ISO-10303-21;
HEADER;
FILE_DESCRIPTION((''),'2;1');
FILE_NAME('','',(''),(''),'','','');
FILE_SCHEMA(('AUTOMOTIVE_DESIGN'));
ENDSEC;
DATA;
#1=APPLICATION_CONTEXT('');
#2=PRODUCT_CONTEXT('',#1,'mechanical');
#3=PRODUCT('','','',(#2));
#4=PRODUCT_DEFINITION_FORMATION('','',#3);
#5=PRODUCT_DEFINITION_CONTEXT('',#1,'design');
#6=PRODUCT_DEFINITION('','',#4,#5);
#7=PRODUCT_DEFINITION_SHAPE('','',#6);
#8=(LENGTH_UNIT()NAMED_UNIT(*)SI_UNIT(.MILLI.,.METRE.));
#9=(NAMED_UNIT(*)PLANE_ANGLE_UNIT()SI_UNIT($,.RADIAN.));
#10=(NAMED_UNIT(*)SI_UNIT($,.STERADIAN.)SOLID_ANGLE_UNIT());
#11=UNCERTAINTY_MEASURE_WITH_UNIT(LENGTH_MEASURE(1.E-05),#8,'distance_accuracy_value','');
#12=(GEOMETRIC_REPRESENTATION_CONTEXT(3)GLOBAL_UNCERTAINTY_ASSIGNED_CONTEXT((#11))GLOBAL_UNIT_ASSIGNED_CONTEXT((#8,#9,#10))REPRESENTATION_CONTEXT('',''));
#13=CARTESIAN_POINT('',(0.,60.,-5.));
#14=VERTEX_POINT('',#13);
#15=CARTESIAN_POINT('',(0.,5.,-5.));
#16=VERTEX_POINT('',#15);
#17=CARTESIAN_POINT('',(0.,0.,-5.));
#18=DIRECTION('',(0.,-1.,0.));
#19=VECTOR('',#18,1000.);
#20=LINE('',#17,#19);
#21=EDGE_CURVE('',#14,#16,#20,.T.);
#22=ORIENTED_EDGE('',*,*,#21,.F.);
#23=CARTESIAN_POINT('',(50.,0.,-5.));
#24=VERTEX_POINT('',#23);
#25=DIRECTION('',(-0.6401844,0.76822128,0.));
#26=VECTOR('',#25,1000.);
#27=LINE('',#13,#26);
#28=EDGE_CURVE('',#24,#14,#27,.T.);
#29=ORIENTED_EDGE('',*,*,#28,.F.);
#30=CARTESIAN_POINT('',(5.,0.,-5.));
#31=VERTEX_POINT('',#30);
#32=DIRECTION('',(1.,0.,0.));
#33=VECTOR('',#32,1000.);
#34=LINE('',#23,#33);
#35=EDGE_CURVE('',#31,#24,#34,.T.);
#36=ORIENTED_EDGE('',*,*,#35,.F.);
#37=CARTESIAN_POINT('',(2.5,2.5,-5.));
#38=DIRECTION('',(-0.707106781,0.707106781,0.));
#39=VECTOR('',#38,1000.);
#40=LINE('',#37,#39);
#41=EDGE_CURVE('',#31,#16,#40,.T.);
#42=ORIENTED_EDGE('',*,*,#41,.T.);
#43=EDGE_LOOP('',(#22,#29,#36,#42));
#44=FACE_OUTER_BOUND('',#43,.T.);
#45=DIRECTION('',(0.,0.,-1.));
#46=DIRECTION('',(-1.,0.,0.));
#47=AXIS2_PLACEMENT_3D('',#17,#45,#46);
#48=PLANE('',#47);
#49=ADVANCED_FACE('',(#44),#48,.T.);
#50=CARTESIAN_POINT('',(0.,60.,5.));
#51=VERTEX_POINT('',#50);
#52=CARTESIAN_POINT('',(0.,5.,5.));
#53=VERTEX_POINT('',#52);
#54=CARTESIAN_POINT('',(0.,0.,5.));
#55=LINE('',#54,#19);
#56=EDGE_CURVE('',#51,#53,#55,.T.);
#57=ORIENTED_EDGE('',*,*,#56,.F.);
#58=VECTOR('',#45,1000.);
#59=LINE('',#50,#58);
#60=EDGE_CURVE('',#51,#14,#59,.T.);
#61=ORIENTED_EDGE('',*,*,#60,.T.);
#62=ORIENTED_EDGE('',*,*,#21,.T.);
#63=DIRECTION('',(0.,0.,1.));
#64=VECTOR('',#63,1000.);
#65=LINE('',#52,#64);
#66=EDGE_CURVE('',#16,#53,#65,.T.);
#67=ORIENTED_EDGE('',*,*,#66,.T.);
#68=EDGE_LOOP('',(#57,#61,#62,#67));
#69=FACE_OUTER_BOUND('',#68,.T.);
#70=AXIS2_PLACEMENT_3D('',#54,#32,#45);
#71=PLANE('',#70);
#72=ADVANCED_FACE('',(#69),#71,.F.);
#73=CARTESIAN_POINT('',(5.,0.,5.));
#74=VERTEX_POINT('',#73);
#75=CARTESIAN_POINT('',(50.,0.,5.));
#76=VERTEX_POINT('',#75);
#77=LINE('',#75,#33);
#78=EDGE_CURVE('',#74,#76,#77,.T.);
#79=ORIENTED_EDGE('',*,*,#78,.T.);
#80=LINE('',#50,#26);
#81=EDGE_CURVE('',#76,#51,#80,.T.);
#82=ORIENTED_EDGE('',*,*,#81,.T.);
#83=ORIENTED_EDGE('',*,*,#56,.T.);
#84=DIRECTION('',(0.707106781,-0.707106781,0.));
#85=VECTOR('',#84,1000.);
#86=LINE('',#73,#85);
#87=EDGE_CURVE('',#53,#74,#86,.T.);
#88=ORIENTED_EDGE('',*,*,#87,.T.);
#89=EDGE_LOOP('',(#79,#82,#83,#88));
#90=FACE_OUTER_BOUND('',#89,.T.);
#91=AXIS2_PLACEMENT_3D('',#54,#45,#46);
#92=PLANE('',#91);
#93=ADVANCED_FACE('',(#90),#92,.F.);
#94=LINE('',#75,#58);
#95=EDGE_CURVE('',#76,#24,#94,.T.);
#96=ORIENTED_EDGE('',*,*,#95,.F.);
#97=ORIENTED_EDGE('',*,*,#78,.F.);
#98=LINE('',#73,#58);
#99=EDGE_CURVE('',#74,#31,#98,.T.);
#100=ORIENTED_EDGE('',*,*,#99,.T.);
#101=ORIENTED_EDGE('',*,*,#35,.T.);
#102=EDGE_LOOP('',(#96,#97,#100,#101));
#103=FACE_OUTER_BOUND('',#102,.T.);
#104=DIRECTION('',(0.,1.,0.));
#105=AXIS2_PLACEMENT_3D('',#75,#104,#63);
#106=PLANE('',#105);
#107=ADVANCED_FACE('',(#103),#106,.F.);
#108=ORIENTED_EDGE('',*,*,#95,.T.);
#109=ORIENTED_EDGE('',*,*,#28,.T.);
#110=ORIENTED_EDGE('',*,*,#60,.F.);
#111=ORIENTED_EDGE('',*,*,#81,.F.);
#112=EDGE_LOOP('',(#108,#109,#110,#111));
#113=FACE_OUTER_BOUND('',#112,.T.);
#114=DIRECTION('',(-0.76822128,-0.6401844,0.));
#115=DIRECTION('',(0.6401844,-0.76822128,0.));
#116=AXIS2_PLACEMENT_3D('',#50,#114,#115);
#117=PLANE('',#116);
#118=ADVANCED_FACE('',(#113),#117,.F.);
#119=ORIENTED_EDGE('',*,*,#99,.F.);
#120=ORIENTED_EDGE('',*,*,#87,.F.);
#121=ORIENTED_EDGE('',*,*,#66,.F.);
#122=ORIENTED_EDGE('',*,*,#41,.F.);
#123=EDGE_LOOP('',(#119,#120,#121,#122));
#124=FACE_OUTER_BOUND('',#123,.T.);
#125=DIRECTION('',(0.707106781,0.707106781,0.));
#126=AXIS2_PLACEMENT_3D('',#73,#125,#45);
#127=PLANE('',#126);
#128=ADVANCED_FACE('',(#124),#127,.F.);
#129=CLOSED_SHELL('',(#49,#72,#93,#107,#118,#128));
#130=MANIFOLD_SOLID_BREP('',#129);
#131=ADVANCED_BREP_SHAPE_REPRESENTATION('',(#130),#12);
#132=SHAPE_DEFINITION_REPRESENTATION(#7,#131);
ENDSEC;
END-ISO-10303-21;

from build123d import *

# Parameters (mm, degrees)
BOSS_EXTRUDE1_DEPTH = 5
CHAMFER1_SIZE       = 5


with BuildPart() as part:
    # Sketch1 → Boss-Extrude1 (new, symmetric)
    with BuildSketch(Plane.XY):
        Polygon((0, 0), (0, 60), (50, 0), align=None)
    extrude(amount=BOSS_EXTRUDE1_DEPTH, both=True)

    # Chamfer1
    chamfer1_edges = [part.edges().sort_by_distance(p)[0] for p in [
        (0, 0, 0),
    ]]
    chamfer(chamfer1_edges, length=CHAMFER1_SIZE)


solid = part.part
